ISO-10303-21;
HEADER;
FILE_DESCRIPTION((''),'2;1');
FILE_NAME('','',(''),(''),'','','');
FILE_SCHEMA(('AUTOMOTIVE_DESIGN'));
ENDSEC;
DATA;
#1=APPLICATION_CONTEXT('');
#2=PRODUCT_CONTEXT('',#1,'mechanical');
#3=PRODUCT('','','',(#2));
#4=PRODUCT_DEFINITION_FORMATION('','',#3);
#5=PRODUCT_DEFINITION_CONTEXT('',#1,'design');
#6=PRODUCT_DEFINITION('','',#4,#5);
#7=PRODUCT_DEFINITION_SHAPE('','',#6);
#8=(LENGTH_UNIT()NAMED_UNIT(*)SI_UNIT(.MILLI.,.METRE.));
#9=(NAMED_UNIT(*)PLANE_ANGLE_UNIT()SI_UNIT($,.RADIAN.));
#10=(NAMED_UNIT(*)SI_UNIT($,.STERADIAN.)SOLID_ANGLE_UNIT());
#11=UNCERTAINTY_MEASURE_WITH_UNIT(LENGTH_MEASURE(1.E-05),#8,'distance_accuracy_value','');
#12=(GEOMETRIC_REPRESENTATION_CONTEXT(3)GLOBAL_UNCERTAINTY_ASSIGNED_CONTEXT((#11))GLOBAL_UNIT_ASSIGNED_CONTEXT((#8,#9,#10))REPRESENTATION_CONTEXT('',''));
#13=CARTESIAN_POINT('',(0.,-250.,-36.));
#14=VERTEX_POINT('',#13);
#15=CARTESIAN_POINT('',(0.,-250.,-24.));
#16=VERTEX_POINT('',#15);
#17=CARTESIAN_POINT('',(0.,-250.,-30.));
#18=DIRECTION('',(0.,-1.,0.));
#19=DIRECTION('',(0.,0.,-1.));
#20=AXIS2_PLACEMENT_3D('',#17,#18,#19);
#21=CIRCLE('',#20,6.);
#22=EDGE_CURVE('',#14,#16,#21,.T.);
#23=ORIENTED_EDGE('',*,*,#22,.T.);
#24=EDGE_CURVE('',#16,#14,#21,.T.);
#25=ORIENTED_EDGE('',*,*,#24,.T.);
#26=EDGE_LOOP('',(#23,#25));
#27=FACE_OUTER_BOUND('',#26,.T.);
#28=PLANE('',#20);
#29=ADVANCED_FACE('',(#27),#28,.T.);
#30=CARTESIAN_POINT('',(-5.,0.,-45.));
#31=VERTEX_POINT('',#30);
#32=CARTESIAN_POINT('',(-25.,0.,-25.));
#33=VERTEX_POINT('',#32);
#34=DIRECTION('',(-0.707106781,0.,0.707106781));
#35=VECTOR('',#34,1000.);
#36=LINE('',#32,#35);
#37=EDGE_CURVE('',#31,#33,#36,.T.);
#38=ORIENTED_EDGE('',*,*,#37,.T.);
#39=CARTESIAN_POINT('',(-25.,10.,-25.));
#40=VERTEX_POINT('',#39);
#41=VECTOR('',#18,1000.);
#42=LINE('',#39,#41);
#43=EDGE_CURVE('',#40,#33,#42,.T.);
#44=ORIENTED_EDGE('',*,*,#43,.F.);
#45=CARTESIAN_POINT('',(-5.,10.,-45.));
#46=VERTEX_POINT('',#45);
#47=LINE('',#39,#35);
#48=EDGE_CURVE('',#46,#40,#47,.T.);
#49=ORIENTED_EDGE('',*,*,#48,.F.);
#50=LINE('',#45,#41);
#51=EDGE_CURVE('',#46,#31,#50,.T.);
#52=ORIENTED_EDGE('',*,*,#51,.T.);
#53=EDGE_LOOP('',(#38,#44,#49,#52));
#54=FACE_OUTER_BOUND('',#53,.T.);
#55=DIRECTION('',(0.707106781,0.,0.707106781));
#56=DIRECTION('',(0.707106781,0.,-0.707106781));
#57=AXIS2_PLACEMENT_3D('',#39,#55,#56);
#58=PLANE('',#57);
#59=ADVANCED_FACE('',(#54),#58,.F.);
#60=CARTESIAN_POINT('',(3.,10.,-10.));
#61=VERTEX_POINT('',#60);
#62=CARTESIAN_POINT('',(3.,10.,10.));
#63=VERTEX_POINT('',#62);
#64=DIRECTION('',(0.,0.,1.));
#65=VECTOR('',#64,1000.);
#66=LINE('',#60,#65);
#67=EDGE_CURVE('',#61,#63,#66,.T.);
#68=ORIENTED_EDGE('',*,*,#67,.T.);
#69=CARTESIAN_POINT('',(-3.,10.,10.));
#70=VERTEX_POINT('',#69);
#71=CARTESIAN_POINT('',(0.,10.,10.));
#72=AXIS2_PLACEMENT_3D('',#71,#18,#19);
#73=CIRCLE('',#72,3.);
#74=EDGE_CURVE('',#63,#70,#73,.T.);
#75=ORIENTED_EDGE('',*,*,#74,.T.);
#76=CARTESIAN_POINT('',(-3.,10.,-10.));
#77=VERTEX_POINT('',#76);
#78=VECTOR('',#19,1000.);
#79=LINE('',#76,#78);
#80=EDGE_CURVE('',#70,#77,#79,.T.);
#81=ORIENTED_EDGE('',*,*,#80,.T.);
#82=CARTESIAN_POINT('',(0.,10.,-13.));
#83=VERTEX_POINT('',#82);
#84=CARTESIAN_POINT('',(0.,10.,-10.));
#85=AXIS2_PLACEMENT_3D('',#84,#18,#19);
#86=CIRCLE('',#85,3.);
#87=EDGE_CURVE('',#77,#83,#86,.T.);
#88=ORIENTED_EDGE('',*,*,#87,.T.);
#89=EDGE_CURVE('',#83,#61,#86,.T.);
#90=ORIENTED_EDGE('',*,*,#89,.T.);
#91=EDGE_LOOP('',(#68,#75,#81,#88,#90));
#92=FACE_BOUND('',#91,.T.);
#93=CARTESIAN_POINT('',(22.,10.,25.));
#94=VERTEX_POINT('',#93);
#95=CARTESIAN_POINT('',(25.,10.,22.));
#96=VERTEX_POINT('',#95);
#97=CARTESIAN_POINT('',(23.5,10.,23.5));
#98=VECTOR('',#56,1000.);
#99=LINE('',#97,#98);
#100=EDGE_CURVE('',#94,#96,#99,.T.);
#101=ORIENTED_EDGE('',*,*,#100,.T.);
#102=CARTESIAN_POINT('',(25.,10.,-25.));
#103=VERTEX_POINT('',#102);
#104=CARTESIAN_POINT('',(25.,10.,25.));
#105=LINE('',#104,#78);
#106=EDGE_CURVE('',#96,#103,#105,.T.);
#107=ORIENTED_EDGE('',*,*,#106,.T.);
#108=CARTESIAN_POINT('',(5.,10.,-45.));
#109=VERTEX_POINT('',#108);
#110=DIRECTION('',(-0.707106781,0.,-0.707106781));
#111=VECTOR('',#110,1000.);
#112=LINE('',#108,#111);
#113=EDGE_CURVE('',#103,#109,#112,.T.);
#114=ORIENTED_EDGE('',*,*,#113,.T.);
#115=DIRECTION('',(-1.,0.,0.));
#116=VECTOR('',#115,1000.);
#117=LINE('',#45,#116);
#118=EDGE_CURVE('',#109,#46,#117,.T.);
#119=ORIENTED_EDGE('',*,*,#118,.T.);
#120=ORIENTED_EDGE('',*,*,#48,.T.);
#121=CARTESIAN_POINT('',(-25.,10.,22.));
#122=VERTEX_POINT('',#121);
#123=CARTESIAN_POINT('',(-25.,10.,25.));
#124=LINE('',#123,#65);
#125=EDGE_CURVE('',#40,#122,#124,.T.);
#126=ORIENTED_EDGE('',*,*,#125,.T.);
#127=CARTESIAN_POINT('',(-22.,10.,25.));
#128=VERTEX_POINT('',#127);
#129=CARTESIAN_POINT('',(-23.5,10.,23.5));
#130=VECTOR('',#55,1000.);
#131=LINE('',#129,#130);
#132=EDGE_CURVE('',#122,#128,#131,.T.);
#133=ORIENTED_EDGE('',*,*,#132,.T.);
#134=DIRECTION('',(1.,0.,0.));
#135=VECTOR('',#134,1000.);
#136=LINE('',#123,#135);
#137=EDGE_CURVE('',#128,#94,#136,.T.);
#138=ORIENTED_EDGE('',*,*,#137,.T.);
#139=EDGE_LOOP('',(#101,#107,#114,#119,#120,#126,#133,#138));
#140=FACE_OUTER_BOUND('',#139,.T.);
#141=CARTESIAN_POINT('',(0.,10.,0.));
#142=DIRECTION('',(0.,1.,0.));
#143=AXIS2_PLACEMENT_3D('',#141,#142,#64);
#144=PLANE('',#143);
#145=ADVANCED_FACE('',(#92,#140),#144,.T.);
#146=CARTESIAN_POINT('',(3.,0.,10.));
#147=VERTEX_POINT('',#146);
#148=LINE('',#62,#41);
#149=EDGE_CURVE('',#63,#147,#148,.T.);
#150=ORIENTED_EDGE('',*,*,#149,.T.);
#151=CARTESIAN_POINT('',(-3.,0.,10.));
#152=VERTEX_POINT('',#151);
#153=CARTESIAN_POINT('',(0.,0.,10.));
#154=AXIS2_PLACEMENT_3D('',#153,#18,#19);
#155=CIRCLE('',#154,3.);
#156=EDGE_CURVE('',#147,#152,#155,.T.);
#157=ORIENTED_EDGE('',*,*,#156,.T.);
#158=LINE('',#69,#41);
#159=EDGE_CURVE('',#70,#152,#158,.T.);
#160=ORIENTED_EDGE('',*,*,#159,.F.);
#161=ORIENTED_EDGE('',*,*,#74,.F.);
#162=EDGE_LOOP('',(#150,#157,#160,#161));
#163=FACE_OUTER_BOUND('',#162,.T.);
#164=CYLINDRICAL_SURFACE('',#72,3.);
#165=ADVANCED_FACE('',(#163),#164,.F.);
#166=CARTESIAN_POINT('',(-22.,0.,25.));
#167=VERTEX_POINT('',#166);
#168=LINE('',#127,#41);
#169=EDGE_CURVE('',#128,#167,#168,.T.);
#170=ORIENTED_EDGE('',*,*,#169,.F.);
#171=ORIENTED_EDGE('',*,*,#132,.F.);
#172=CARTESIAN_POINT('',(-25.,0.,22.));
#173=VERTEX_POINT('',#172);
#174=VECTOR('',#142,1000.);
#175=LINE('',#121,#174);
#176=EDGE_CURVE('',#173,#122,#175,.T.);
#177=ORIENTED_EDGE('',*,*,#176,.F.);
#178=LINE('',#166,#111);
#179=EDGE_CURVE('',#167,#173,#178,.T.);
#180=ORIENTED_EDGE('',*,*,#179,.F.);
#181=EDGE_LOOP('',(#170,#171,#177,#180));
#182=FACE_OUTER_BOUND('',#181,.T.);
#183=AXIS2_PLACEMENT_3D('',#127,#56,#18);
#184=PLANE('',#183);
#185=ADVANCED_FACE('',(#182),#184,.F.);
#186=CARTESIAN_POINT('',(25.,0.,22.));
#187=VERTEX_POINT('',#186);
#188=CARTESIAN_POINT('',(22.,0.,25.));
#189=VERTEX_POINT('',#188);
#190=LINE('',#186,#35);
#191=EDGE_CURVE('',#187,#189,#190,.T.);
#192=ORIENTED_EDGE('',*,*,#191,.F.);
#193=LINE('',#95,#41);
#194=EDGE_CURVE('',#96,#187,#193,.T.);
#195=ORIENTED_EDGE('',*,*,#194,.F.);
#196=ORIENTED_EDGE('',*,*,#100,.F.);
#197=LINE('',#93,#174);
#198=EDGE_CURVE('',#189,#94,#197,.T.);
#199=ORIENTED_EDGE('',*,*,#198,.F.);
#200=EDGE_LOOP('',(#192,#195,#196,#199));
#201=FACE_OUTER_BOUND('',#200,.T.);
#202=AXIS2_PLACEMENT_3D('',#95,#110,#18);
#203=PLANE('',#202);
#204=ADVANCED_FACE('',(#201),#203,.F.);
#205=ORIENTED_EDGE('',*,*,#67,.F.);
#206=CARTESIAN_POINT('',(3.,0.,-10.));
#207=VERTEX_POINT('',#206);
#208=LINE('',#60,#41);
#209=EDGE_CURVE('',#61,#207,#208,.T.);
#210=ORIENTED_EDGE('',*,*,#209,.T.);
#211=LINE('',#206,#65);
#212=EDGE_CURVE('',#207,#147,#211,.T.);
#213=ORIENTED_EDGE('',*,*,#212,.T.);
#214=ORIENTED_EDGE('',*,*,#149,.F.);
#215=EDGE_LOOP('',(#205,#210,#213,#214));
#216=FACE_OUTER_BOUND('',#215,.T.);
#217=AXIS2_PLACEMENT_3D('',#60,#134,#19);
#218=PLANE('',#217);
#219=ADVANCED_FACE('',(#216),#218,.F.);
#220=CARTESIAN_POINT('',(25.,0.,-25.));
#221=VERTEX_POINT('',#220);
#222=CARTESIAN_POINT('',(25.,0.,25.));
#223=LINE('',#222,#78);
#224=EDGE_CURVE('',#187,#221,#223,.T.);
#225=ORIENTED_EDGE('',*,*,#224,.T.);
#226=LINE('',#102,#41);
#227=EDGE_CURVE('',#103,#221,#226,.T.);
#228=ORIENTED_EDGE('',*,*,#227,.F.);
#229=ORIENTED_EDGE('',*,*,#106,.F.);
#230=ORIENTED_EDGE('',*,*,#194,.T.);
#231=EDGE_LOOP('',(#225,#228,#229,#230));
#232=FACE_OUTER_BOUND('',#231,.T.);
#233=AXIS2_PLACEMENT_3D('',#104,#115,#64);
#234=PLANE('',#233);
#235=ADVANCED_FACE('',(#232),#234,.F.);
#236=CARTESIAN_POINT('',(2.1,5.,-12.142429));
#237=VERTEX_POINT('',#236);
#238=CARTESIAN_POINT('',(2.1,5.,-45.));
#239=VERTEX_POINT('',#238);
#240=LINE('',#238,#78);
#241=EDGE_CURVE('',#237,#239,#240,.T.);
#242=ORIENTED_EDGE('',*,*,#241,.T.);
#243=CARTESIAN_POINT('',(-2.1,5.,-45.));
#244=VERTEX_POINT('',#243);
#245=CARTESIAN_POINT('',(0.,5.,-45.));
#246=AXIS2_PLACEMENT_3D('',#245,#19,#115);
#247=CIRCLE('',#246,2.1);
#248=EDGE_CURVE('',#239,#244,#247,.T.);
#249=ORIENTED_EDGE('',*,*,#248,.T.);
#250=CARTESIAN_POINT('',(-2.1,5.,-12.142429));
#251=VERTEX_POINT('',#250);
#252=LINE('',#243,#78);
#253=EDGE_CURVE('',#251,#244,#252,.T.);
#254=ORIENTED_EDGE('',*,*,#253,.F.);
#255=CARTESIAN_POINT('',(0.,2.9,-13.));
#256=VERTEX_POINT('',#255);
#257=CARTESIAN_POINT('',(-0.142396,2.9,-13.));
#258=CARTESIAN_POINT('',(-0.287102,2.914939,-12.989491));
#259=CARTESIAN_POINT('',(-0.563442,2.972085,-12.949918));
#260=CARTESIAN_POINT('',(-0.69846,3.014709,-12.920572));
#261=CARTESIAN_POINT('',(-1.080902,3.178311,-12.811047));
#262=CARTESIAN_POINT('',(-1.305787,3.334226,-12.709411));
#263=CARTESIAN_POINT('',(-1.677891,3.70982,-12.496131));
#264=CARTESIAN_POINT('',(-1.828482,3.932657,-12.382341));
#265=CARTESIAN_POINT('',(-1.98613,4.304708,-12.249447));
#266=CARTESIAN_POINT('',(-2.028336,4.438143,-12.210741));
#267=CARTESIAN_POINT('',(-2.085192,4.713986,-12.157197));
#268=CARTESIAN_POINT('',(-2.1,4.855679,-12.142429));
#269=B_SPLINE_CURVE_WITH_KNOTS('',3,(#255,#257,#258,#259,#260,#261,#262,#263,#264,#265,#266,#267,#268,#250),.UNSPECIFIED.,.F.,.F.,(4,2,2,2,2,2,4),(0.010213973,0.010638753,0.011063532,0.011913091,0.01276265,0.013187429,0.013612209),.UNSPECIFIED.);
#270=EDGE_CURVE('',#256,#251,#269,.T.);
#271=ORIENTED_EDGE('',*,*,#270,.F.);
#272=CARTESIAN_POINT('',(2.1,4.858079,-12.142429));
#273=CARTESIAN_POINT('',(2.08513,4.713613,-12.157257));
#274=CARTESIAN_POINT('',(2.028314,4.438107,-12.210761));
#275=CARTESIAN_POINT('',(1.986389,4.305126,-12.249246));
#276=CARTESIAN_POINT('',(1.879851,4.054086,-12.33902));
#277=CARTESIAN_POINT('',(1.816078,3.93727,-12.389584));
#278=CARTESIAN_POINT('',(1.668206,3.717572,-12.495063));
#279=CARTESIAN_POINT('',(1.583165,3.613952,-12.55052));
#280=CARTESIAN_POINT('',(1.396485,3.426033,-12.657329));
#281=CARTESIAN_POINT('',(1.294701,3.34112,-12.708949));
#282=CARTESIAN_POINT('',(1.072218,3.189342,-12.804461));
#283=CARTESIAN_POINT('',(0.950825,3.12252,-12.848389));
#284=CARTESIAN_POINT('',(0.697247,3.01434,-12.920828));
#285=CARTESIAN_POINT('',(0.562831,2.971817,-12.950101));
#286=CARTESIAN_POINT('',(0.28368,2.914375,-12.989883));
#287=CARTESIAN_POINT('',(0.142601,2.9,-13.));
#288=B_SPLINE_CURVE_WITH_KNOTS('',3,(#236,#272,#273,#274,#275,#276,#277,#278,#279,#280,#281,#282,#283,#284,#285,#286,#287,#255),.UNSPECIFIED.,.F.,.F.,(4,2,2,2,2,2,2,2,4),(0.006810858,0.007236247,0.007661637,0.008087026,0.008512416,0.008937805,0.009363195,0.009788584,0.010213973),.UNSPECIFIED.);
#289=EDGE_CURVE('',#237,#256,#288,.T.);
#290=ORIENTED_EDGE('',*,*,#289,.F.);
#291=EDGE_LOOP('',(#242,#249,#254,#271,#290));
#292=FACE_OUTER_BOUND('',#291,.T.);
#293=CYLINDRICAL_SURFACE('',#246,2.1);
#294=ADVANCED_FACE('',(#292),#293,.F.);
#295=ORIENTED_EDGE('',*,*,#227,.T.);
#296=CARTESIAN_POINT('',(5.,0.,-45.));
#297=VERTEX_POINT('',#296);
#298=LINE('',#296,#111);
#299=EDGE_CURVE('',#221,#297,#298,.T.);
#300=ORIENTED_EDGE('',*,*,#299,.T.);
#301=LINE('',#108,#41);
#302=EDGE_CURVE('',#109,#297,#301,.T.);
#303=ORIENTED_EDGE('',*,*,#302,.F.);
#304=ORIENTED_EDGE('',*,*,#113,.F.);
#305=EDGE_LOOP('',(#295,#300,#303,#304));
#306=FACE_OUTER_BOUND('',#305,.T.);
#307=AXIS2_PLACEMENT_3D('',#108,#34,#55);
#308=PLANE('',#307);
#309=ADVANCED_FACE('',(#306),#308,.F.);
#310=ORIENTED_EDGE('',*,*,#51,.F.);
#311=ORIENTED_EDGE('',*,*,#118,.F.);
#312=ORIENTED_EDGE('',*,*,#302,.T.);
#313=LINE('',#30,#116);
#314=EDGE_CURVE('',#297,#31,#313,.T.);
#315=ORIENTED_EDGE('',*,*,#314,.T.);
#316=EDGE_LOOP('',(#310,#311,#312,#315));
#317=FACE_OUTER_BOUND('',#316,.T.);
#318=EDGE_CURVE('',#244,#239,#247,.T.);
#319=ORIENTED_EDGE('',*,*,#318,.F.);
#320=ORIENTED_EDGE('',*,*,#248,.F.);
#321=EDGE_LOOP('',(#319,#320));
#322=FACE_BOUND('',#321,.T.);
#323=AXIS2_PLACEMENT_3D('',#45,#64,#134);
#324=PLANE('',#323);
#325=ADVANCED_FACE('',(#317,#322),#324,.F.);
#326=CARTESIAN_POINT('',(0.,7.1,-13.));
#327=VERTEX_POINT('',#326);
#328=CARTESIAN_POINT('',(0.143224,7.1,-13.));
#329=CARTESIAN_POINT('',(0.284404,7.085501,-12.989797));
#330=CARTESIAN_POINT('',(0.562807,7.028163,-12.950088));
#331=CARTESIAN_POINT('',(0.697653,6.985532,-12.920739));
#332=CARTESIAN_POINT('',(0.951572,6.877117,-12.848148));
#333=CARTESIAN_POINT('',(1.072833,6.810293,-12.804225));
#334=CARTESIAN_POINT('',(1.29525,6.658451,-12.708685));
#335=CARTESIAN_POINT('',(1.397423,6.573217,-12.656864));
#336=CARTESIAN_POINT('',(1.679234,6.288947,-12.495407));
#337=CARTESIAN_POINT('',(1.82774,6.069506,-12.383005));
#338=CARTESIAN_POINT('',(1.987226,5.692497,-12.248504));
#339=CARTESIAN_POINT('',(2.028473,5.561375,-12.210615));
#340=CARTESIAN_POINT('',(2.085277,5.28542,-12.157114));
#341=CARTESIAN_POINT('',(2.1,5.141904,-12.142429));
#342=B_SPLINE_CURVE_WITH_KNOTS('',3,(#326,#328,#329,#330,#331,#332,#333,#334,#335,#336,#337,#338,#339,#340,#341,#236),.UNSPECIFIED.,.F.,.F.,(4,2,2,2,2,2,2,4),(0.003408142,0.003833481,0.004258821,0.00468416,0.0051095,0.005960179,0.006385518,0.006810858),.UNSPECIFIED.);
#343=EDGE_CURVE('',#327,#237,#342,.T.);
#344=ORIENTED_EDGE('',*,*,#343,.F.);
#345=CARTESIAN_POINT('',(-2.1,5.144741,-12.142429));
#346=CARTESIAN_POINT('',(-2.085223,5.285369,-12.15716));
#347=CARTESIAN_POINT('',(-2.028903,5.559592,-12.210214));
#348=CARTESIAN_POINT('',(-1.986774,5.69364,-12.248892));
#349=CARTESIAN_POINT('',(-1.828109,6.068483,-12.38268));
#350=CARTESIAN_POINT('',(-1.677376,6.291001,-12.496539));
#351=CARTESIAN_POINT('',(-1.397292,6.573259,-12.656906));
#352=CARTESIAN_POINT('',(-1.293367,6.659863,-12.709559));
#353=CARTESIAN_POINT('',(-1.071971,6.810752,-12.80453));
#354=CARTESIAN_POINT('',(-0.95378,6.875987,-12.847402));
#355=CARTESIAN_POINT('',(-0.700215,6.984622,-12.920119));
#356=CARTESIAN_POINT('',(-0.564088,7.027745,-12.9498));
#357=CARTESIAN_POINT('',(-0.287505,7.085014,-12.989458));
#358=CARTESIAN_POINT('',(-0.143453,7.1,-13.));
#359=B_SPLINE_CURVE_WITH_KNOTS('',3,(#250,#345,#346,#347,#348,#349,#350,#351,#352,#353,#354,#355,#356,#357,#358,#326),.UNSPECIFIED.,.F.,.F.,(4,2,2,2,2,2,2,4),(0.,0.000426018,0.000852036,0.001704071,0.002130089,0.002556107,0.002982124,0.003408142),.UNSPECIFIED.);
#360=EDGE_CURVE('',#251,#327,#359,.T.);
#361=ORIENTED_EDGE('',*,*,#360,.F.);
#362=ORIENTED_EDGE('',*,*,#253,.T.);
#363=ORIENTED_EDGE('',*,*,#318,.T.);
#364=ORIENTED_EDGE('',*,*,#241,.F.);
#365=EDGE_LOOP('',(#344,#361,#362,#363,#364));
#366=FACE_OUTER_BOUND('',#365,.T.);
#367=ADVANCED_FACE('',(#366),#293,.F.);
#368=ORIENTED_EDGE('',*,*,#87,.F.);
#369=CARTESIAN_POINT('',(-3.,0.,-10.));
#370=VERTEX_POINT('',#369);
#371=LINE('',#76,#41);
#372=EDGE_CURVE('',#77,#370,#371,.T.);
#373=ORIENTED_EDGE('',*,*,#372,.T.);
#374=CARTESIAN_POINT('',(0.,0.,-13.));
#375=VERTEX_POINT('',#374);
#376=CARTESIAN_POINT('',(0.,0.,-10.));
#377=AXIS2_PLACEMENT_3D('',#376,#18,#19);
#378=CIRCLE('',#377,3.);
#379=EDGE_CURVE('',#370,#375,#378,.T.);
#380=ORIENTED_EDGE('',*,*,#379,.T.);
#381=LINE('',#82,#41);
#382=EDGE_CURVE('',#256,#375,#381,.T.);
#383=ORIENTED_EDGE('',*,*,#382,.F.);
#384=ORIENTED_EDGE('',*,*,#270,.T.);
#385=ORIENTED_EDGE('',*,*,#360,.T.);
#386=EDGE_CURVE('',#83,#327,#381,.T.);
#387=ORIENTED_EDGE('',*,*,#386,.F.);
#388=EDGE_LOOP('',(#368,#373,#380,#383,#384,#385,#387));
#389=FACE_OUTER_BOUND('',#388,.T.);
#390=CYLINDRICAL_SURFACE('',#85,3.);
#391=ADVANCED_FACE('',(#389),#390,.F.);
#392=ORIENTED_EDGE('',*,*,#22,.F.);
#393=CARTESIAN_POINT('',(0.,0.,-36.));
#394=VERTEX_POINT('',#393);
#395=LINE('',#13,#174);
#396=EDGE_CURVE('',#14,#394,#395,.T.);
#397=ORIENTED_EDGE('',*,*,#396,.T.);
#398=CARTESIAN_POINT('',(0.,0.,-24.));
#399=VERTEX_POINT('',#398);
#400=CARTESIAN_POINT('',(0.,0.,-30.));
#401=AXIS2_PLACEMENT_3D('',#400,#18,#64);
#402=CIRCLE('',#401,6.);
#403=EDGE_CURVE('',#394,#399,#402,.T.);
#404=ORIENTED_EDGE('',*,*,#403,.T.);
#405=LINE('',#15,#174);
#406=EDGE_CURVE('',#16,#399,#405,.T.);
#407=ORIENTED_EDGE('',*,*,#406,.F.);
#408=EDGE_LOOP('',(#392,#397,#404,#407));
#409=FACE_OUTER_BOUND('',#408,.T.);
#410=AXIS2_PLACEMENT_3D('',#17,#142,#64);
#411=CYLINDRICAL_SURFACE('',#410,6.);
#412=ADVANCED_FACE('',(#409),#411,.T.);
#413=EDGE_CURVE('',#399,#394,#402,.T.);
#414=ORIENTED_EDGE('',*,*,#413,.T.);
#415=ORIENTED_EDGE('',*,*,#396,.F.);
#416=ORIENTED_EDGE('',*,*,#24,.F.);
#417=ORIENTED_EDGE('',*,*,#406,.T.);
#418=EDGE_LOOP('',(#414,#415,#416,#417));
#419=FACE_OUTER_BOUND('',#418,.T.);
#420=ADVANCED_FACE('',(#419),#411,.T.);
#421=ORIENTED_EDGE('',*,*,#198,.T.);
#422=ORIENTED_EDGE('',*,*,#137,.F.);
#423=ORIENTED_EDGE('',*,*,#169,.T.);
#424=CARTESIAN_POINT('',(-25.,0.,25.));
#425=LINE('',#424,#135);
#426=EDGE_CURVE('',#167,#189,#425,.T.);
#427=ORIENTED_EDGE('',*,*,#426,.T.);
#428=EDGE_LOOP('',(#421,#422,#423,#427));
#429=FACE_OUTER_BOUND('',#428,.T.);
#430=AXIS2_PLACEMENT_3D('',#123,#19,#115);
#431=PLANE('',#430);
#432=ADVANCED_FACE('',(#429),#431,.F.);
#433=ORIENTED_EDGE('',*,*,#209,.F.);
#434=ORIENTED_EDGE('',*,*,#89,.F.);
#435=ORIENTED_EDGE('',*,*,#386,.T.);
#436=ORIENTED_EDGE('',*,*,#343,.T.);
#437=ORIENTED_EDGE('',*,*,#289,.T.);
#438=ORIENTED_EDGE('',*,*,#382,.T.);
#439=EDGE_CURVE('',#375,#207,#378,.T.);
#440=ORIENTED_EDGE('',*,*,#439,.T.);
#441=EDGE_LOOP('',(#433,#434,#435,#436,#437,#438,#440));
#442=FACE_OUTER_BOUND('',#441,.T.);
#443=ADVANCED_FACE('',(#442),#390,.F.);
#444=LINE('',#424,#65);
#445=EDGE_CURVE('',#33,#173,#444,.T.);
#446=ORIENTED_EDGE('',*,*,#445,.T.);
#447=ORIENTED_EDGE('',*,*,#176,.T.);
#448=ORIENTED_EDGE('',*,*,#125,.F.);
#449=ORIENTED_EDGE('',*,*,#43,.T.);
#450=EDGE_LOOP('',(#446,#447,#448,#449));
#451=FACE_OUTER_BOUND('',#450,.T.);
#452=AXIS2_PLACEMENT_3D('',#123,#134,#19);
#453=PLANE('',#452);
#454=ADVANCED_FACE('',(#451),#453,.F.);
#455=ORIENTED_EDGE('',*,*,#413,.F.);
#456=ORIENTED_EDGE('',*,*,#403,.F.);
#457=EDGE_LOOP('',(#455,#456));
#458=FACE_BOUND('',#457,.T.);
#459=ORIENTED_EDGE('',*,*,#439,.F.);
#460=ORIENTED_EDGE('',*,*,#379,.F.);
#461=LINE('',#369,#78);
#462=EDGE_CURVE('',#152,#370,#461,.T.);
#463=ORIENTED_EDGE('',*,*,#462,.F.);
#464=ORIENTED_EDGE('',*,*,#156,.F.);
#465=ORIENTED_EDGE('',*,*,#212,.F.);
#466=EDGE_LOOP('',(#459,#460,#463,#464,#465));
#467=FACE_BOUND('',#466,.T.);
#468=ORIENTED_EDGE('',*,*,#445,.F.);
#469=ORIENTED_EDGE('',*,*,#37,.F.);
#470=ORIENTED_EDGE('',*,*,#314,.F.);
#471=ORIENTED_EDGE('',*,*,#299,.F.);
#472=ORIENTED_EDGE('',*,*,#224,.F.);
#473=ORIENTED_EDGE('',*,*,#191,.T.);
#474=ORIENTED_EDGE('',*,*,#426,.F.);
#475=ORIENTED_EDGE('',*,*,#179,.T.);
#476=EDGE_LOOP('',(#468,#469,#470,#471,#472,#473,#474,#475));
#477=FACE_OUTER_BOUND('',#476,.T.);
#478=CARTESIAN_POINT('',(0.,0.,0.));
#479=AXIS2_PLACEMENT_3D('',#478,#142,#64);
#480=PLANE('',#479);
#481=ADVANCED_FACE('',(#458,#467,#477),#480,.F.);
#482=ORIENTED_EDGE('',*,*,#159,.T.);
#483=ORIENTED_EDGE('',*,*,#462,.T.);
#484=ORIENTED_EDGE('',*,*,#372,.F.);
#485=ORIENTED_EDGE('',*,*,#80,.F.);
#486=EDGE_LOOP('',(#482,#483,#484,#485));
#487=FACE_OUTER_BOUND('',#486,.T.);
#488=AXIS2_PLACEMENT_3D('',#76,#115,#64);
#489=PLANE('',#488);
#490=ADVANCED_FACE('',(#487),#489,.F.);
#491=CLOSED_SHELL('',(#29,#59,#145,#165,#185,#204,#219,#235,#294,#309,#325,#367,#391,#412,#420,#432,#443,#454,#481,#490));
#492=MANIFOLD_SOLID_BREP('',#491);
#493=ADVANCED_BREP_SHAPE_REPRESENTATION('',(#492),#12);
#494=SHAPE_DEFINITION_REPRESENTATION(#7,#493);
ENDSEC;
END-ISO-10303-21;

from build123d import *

# Parameters (mm, degrees)
BOSS_EXTRUDE1_DEPTH   = 10
SKETCH2_R             = 6
BOSS_EXTRUDE2_DEPTH   = 260
CUT_EXTRUDE1_DEPTH    = 256.244980362
M5_TAPPED_HOLE1_D     = 4.2
M5_TAPPED_HOLE1_DEPTH = 36.9
M5_TAPPED_HOLE1_TIP   = 1.2618073
CHAMFER1_SIZE         = 3


with BuildPart() as part:
    # Sketch1 → Boss-Extrude1 (new body)
    with BuildSketch(Plane(origin=(0, 0, 0), x_dir=(1, 0, 0), z_dir=(0, 1, 0))):
        Polygon((-25, 25), (-5, 45), (5, 45), (25, 25), (25, -25), (-25, -25), align=None)
    extrude(amount=BOSS_EXTRUDE1_DEPTH)

    # Sketch2 → Boss-Extrude2 (add)
    with BuildSketch(Plane.XZ.offset(-10)):
        with Locations(Location((0, -30, 0), (0, 0, 90))):
            Circle(SKETCH2_R)
    extrude(amount=BOSS_EXTRUDE2_DEPTH)

    # Sketch3 → Cut-Extrude1 (cut, through all)
    with BuildSketch(Plane.XZ):
        with BuildLine():
            Line((-3, -10), (-3, 10))
            ThreePointArc((-3, 10), (0, 13), (3, 10))
            Line((3, 10), (3, -10))
            ThreePointArc((3, -10), (0, -13), (-3, -10))
        make_face()
    extrude(amount=-CUT_EXTRUDE1_DEPTH, mode=Mode.SUBTRACT)

    # M5 Tapped Hole1
    with Locations(Plane(origin=(0, 0, -45), x_dir=(-1, 0, 0), z_dir=(0, 0, -1))):
        with Locations((0, 5)):
            Hole(M5_TAPPED_HOLE1_D / 2, depth=M5_TAPPED_HOLE1_DEPTH)
            with Locations((0, 0, -(M5_TAPPED_HOLE1_DEPTH + M5_TAPPED_HOLE1_TIP / 2))):  # 118° drill point
                Cone(0, M5_TAPPED_HOLE1_D / 2, M5_TAPPED_HOLE1_TIP, mode=Mode.SUBTRACT)

    # Chamfer1
    chamfer1_edges = [part.edges().sort_by_distance(p)[0] for p in [
        (25, 5, 25),
        (-25, 5, 25),
    ]]
    chamfer(chamfer1_edges, length=CHAMFER1_SIZE)


solid = part.part
